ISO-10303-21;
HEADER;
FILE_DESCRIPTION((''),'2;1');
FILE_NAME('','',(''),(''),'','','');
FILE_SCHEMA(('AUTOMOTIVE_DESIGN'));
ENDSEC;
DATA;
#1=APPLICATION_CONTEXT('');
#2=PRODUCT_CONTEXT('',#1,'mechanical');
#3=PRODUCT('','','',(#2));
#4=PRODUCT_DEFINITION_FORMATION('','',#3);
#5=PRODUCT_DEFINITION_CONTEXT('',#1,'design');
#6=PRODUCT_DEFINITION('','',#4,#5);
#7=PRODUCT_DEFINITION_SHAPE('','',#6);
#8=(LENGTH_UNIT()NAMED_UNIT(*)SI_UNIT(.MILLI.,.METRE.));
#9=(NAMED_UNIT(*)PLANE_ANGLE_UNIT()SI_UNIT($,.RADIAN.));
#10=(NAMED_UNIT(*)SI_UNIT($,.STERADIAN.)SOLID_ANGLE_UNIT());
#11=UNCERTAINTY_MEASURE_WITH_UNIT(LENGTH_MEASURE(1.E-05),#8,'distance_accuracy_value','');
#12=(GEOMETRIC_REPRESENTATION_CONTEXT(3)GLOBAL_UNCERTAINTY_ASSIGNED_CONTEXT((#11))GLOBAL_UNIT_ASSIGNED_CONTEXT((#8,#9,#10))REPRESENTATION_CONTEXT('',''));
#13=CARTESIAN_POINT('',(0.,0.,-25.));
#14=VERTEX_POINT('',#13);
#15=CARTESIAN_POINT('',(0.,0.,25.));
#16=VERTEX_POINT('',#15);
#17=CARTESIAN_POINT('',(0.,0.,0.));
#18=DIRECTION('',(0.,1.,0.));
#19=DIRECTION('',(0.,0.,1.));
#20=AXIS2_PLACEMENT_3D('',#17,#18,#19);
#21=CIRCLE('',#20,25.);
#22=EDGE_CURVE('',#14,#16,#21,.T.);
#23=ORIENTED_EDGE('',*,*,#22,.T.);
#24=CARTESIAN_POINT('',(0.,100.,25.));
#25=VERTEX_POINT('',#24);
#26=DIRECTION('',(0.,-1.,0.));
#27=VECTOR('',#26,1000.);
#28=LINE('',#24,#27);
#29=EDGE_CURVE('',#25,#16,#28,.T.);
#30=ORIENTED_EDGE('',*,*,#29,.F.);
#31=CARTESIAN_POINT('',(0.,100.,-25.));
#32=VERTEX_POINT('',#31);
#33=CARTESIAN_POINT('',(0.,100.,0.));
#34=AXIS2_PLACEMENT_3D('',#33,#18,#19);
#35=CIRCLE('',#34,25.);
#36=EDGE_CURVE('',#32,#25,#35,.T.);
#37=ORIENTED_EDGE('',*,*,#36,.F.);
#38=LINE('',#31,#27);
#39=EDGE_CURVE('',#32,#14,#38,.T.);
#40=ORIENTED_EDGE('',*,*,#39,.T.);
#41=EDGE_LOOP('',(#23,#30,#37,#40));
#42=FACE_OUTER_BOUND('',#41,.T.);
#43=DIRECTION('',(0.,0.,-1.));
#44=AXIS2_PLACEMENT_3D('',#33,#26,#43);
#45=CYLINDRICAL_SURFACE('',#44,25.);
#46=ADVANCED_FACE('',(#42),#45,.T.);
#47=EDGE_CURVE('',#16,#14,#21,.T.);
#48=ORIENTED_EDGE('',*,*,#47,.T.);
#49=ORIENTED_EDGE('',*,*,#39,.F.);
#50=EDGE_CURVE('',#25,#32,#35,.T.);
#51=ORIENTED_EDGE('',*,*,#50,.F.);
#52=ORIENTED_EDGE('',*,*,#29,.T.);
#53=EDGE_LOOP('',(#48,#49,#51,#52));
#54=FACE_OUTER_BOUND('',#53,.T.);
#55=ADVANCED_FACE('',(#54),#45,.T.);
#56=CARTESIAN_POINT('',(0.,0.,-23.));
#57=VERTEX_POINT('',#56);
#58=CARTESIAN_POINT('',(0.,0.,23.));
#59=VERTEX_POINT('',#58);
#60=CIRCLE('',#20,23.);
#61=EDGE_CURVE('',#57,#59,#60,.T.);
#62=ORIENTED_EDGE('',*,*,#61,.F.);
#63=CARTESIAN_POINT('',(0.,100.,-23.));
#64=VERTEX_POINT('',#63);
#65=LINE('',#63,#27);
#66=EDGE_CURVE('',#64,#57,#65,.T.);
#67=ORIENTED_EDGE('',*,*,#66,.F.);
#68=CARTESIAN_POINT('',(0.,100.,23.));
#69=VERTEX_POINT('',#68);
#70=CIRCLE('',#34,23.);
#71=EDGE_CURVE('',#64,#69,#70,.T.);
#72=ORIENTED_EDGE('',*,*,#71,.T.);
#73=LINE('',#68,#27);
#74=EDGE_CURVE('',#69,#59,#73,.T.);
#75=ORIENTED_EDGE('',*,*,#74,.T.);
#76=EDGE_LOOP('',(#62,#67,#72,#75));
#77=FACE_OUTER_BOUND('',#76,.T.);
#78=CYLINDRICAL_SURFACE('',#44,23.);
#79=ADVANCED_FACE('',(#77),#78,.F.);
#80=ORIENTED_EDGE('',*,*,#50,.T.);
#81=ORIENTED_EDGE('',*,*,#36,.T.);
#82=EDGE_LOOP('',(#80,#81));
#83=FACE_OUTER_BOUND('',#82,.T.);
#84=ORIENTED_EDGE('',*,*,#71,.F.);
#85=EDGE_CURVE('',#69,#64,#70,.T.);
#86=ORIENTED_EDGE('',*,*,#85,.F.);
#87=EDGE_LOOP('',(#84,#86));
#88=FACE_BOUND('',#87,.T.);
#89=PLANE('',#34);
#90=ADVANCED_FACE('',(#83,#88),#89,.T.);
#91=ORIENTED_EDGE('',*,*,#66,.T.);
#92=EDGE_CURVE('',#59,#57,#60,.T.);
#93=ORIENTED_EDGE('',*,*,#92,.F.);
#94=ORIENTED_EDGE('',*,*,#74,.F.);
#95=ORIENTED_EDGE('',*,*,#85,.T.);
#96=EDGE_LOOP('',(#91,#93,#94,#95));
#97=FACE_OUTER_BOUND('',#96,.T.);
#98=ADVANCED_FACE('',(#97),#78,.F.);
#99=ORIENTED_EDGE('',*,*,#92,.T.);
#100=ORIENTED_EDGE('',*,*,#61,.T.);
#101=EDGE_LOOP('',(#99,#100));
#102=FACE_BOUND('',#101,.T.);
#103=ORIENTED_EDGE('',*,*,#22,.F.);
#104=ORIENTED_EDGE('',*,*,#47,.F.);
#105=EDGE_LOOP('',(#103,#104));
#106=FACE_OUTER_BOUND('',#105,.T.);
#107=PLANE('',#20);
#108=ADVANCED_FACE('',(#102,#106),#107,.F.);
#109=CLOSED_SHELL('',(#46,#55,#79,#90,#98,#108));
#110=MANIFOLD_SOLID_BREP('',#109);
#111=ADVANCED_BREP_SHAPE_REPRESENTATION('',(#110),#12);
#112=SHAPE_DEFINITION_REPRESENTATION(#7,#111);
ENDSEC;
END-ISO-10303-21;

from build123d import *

# Parameters (mm, degrees)
SKETCH1_R           = 25
SKETCH1_R_2         = 23
BOSS_EXTRUDE1_DEPTH = 100


with BuildPart() as part:
    # Sketch1 → Boss-Extrude1 (new body)
    with BuildSketch(Plane(origin=(0, 0, 0), x_dir=(1, 0, 0), z_dir=(0, 1, 0))):
        with Locations(Location((0, 0, 0), (0, 0, 270))):
            Circle(SKETCH1_R)
        with Locations(Location((0, 0, 0), (0, 0, 270))):
            Circle(SKETCH1_R_2, mode=Mode.SUBTRACT)
    extrude(amount=BOSS_EXTRUDE1_DEPTH)


solid = part.part
